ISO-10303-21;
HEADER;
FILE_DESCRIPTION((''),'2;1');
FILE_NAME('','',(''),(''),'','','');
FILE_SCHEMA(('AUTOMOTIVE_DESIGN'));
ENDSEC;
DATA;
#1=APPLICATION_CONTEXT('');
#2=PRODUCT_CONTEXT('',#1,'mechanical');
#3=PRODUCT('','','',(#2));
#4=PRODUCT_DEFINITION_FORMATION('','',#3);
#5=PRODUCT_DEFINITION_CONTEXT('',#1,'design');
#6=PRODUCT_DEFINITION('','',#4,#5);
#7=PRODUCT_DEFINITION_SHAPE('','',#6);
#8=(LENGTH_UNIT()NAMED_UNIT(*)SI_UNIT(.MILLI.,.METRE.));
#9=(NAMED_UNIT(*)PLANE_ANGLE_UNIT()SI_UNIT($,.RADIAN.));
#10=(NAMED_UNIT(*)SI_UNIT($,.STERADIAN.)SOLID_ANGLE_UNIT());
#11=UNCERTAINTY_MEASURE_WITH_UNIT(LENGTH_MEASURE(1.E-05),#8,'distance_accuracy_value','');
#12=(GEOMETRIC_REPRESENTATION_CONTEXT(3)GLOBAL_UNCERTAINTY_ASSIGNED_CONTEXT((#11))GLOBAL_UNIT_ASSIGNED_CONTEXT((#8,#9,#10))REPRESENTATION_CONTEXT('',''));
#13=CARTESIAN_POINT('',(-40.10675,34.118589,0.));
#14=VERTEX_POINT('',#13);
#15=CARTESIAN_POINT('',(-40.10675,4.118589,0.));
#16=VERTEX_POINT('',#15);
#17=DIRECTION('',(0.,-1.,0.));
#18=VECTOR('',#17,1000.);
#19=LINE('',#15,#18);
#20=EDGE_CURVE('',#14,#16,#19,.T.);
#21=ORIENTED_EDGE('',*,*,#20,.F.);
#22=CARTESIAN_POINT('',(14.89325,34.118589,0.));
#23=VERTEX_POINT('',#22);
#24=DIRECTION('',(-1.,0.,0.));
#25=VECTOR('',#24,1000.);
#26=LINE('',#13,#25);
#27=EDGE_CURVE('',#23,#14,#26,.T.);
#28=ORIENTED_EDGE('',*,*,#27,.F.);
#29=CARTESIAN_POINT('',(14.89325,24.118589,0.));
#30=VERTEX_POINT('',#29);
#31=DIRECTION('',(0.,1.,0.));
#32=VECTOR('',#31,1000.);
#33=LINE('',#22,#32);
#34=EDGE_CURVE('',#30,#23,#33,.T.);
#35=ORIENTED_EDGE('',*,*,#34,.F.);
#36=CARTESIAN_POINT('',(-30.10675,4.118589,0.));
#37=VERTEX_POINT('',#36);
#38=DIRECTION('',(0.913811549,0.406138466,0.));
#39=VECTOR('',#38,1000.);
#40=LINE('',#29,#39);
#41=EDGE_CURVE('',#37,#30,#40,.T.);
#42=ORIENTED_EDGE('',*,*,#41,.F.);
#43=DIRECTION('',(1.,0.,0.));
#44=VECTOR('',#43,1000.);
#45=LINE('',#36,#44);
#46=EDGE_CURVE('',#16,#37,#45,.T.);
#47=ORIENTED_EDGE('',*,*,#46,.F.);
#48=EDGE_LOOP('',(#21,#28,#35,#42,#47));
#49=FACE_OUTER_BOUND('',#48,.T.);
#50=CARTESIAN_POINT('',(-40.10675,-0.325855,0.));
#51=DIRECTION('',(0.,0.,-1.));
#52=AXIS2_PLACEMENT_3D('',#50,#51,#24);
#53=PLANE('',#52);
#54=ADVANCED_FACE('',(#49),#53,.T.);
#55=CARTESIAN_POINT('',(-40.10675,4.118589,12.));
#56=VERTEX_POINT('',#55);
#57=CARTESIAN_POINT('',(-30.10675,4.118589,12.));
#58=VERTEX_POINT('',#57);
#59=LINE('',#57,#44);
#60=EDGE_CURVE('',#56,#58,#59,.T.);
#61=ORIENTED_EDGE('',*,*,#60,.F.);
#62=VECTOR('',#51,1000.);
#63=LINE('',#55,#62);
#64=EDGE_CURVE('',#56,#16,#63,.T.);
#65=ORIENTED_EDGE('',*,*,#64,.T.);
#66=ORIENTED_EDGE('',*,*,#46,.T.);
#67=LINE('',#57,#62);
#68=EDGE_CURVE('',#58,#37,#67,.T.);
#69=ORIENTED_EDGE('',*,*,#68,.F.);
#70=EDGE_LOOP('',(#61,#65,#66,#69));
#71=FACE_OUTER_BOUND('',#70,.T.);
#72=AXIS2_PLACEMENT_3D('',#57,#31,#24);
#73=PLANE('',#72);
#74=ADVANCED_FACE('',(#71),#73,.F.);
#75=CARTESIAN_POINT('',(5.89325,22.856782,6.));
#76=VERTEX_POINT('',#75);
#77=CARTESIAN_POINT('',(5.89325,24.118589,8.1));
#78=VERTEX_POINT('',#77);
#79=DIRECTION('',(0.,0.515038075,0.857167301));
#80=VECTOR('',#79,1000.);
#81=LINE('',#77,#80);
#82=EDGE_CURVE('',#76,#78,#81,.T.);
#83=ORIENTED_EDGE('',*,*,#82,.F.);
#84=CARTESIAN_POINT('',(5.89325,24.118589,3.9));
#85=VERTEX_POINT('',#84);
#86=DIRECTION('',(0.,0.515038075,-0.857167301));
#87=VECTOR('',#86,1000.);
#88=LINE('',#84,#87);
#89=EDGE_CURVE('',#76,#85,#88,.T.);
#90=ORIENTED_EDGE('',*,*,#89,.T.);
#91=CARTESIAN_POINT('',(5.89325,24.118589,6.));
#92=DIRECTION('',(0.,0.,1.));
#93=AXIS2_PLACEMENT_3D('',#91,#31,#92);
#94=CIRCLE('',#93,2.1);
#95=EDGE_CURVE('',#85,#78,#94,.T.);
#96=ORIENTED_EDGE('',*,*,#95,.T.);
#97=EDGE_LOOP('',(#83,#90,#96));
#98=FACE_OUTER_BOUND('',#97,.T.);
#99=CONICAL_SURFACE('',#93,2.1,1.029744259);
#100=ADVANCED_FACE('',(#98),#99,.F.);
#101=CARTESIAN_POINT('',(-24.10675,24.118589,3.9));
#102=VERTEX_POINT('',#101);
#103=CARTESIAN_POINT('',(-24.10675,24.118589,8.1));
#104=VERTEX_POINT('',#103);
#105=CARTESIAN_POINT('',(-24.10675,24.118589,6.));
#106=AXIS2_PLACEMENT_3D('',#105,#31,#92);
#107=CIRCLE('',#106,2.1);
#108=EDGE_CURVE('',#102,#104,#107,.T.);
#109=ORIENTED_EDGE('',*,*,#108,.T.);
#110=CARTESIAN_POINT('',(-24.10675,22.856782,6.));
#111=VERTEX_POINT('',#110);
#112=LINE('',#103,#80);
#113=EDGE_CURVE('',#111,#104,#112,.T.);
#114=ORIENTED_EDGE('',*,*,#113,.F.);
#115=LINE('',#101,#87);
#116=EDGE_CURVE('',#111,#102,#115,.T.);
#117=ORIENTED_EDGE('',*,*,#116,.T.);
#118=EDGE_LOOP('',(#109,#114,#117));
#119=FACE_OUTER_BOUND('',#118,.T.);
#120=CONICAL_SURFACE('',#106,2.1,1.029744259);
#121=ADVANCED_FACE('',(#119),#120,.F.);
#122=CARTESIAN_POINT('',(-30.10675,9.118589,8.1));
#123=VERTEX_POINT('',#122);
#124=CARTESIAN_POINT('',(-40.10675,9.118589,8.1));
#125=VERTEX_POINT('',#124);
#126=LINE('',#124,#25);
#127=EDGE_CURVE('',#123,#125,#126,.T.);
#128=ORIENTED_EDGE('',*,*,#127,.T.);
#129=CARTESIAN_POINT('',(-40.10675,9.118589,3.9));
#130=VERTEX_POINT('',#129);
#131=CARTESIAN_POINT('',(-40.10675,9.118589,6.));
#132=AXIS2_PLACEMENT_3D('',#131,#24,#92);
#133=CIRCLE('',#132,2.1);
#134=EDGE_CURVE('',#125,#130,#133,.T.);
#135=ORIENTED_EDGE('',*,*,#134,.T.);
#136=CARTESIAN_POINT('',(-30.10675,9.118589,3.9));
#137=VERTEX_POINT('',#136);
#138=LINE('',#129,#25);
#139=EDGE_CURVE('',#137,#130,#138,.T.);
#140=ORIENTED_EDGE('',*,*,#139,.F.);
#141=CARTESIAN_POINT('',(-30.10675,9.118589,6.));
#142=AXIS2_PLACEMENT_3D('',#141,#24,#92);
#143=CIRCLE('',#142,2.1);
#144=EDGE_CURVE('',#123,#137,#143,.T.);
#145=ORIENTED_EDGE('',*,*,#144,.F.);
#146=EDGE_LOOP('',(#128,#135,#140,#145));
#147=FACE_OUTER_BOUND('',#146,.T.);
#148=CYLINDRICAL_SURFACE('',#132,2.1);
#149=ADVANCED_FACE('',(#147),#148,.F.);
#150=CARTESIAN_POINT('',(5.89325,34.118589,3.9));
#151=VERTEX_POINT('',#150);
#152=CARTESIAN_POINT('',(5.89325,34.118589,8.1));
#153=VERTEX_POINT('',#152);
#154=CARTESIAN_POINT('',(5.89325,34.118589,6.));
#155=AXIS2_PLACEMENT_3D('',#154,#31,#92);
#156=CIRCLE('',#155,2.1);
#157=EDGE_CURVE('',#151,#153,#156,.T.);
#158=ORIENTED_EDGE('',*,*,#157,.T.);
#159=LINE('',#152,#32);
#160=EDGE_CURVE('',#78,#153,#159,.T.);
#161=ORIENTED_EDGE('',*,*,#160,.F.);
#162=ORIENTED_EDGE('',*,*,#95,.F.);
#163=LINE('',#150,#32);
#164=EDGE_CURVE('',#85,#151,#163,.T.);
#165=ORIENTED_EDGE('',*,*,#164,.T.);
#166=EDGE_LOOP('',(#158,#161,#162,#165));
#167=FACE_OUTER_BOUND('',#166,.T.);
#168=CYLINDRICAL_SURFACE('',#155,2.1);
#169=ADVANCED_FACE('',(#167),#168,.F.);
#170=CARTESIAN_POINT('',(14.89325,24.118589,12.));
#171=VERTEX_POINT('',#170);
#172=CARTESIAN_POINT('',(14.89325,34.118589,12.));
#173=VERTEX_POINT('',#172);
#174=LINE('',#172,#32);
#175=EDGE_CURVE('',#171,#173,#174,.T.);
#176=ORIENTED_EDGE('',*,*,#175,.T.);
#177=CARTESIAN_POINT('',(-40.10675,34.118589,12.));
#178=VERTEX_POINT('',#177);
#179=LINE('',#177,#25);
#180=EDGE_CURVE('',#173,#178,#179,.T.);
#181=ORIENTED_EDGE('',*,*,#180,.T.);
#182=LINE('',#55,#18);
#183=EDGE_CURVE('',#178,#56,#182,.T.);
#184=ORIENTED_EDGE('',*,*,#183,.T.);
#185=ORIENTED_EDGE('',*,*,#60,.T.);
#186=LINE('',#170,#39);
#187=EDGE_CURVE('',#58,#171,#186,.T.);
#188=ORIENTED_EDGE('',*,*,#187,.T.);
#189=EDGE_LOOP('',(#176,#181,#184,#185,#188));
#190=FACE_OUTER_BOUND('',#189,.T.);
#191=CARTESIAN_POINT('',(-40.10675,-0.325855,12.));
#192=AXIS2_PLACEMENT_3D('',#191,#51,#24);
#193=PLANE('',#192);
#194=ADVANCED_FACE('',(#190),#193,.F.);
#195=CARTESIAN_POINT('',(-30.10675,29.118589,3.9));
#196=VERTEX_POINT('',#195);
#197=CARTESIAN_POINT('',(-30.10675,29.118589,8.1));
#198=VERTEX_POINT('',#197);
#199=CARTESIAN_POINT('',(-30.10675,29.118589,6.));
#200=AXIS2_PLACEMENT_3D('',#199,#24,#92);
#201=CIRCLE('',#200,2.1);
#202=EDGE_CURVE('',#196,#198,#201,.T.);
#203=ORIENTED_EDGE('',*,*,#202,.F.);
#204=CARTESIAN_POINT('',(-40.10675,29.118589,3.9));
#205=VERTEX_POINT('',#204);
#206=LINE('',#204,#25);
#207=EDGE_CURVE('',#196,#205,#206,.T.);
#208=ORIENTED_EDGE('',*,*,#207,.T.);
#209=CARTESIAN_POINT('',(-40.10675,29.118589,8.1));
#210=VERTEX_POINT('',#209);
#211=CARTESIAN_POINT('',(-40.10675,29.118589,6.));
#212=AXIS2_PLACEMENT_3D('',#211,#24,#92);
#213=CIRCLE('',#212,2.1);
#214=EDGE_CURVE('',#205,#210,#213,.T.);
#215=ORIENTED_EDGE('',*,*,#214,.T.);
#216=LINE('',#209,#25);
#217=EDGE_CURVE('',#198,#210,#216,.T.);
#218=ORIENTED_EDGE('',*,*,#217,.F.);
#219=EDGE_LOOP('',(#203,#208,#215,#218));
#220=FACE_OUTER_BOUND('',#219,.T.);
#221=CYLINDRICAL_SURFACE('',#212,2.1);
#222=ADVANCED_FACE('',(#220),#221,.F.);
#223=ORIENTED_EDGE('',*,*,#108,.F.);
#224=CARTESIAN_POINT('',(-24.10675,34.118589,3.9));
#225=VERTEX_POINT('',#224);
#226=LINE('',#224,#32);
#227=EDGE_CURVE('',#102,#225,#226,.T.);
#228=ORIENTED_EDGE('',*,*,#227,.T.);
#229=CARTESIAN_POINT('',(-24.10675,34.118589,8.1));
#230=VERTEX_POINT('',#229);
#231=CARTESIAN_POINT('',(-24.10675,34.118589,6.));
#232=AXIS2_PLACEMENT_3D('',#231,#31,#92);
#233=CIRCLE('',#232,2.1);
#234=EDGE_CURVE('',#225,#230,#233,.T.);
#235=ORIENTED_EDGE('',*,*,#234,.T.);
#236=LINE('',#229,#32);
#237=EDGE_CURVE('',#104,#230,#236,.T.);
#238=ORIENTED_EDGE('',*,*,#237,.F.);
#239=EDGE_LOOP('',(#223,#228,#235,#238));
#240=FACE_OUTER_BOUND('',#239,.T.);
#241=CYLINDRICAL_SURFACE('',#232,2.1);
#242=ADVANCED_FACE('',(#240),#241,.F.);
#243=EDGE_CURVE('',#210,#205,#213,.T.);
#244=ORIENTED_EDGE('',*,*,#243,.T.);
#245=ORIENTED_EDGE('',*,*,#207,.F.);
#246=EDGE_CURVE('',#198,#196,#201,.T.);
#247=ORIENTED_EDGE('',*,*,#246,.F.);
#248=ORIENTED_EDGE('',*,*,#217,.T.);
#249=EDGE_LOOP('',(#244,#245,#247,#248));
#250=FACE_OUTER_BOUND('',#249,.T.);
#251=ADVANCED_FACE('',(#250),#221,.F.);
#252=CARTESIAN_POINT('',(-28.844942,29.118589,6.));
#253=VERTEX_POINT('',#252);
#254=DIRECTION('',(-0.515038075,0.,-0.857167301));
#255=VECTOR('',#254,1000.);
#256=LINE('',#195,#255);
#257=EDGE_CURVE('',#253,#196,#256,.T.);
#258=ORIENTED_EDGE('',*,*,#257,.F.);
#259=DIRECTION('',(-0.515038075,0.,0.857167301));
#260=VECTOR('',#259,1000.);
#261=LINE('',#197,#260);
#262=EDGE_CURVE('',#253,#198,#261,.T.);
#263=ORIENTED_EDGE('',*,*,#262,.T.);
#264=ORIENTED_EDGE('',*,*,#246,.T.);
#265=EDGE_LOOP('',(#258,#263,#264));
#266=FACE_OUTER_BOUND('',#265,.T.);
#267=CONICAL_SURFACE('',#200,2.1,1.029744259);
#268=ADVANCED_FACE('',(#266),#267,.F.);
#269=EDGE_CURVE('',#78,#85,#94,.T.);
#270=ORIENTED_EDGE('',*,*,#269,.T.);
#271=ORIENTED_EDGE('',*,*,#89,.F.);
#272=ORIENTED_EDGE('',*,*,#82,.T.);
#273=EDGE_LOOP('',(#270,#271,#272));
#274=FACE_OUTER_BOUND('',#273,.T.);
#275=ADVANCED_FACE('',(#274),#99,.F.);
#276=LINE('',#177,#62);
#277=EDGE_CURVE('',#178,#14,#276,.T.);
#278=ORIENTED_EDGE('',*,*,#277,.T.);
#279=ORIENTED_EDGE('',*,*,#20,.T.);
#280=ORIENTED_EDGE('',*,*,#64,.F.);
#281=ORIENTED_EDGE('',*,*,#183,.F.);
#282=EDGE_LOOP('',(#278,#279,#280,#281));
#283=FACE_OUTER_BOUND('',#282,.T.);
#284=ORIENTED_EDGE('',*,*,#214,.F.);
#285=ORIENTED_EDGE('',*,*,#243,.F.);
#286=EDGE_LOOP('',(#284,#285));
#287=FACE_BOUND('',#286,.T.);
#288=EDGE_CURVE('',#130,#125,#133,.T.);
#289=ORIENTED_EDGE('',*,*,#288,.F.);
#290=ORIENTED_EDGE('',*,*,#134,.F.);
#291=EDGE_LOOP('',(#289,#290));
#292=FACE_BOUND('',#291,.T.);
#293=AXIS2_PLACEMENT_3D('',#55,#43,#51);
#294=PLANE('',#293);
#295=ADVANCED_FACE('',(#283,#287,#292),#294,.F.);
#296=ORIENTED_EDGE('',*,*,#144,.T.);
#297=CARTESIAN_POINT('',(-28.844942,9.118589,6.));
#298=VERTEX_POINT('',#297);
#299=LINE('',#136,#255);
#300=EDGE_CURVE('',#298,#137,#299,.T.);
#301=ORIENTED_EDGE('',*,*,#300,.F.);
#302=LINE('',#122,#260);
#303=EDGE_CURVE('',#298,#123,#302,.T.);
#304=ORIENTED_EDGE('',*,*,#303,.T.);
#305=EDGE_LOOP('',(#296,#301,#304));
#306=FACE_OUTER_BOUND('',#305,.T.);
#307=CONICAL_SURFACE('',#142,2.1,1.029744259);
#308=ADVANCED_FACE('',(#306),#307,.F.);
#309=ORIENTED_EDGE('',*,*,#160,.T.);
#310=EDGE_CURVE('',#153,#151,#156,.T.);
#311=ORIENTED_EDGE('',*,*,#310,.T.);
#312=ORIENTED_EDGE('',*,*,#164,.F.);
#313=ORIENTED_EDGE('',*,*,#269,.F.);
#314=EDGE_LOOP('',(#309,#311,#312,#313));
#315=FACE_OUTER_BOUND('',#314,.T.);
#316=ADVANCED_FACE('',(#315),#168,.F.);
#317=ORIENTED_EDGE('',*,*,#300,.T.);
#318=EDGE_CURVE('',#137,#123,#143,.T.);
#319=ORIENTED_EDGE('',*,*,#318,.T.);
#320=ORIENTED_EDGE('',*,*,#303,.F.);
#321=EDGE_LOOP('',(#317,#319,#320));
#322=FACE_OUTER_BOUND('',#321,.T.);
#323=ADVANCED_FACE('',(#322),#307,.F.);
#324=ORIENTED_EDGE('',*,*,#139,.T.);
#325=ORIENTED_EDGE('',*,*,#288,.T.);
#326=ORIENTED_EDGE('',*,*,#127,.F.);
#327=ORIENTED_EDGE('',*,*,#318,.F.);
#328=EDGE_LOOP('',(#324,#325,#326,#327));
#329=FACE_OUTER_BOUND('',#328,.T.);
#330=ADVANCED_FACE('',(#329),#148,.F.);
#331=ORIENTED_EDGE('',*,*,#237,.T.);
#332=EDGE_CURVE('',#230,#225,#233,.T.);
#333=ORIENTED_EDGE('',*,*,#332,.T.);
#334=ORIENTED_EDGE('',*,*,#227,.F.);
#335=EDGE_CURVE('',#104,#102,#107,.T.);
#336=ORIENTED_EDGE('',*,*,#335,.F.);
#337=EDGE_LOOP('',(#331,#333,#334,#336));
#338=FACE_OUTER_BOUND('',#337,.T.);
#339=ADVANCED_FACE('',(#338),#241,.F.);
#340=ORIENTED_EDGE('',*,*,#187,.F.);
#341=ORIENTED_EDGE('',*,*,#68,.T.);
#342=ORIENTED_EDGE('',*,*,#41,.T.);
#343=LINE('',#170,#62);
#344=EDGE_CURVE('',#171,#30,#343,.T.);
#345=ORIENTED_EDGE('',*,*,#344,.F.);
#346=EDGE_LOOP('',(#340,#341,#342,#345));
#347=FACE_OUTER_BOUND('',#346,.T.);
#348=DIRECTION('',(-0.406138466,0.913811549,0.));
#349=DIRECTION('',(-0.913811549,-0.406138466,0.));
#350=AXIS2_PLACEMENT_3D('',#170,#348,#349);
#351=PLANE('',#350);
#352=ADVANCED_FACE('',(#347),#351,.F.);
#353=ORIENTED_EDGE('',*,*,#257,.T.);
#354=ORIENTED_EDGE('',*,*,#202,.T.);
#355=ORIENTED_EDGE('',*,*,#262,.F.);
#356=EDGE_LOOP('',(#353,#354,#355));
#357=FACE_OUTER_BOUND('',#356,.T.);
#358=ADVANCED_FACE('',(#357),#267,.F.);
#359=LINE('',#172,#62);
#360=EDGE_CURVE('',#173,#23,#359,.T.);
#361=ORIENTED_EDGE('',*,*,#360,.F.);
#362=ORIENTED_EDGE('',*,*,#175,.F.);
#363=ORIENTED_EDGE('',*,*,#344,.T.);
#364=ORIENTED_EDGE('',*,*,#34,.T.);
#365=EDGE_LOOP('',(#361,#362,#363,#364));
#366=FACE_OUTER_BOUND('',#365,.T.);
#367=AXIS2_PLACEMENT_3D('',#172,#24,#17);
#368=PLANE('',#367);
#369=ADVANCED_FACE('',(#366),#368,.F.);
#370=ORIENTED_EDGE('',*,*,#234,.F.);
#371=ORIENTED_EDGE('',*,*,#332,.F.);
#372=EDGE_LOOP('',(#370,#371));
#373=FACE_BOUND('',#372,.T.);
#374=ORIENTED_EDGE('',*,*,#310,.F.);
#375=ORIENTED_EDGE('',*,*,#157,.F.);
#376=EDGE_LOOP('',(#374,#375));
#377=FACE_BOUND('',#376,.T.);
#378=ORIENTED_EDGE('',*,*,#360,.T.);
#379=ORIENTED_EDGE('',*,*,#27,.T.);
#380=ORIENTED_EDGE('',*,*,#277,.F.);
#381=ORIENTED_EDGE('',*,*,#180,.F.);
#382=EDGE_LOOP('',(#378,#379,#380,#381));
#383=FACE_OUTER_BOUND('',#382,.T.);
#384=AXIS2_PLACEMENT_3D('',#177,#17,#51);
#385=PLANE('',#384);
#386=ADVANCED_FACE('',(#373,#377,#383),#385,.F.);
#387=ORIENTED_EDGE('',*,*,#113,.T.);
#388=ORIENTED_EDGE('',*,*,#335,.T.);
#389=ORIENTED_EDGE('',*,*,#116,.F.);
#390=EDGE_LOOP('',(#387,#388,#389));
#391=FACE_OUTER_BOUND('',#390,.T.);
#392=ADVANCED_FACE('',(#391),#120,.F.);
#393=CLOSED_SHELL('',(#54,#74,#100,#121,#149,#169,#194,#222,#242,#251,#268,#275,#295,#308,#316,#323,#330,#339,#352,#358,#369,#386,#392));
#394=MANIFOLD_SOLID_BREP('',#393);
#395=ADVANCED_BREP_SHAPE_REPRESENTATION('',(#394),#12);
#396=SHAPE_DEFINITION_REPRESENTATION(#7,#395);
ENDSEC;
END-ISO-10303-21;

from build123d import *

# Parameters (mm, degrees)
EXTRUDE_1_DEPTH        = 12
HOLE_WIZARD_M5_1_D     = 4.2
HOLE_WIZARD_M5_1_DEPTH = 10
HOLE_WIZARD_M5_1_TIP   = 1.2618073
HOLE_WIZARD_M5_2_D     = 4.2
HOLE_WIZARD_M5_2_DEPTH = 10
HOLE_WIZARD_M5_2_TIP   = 1.2618073


with BuildPart() as part:
    # 草图1 → 凸台-拉伸1 (new body)
    with BuildSketch(Plane.XY):
        Polygon((-30.106749708, 4.118589161), (-40.106749708, 4.118589161), (-40.106749708, 34.118589161), (14.893250292, 34.118589161), (14.893250292, 24.118589161), align=None)
    extrude(amount=EXTRUDE_1_DEPTH)

    # M5 螺纹孔1
    with Locations(Plane(origin=(-24.106749708, 34.118589161, 6), x_dir=(0, 0, 1), z_dir=(0, 1, 0))):
        with Locations((0, 0), (0, 30)):
            Hole(HOLE_WIZARD_M5_1_D / 2, depth=HOLE_WIZARD_M5_1_DEPTH)
            with Locations((0, 0, -(HOLE_WIZARD_M5_1_DEPTH + HOLE_WIZARD_M5_1_TIP / 2))):  # 118° drill point
                Cone(0, HOLE_WIZARD_M5_1_D / 2, HOLE_WIZARD_M5_1_TIP, mode=Mode.SUBTRACT)

    # M5 螺纹孔2
    with Locations(Plane(origin=(-40.106749708, 9.118589161, 6), x_dir=(0, 0, -1), z_dir=(-1, 0, 0))):
        with Locations((0, 0), (0, -20)):
            Hole(HOLE_WIZARD_M5_2_D / 2, depth=HOLE_WIZARD_M5_2_DEPTH)
            with Locations((0, 0, -(HOLE_WIZARD_M5_2_DEPTH + HOLE_WIZARD_M5_2_TIP / 2))):  # 118° drill point
                Cone(0, HOLE_WIZARD_M5_2_D / 2, HOLE_WIZARD_M5_2_TIP, mode=Mode.SUBTRACT)


solid = part.part
